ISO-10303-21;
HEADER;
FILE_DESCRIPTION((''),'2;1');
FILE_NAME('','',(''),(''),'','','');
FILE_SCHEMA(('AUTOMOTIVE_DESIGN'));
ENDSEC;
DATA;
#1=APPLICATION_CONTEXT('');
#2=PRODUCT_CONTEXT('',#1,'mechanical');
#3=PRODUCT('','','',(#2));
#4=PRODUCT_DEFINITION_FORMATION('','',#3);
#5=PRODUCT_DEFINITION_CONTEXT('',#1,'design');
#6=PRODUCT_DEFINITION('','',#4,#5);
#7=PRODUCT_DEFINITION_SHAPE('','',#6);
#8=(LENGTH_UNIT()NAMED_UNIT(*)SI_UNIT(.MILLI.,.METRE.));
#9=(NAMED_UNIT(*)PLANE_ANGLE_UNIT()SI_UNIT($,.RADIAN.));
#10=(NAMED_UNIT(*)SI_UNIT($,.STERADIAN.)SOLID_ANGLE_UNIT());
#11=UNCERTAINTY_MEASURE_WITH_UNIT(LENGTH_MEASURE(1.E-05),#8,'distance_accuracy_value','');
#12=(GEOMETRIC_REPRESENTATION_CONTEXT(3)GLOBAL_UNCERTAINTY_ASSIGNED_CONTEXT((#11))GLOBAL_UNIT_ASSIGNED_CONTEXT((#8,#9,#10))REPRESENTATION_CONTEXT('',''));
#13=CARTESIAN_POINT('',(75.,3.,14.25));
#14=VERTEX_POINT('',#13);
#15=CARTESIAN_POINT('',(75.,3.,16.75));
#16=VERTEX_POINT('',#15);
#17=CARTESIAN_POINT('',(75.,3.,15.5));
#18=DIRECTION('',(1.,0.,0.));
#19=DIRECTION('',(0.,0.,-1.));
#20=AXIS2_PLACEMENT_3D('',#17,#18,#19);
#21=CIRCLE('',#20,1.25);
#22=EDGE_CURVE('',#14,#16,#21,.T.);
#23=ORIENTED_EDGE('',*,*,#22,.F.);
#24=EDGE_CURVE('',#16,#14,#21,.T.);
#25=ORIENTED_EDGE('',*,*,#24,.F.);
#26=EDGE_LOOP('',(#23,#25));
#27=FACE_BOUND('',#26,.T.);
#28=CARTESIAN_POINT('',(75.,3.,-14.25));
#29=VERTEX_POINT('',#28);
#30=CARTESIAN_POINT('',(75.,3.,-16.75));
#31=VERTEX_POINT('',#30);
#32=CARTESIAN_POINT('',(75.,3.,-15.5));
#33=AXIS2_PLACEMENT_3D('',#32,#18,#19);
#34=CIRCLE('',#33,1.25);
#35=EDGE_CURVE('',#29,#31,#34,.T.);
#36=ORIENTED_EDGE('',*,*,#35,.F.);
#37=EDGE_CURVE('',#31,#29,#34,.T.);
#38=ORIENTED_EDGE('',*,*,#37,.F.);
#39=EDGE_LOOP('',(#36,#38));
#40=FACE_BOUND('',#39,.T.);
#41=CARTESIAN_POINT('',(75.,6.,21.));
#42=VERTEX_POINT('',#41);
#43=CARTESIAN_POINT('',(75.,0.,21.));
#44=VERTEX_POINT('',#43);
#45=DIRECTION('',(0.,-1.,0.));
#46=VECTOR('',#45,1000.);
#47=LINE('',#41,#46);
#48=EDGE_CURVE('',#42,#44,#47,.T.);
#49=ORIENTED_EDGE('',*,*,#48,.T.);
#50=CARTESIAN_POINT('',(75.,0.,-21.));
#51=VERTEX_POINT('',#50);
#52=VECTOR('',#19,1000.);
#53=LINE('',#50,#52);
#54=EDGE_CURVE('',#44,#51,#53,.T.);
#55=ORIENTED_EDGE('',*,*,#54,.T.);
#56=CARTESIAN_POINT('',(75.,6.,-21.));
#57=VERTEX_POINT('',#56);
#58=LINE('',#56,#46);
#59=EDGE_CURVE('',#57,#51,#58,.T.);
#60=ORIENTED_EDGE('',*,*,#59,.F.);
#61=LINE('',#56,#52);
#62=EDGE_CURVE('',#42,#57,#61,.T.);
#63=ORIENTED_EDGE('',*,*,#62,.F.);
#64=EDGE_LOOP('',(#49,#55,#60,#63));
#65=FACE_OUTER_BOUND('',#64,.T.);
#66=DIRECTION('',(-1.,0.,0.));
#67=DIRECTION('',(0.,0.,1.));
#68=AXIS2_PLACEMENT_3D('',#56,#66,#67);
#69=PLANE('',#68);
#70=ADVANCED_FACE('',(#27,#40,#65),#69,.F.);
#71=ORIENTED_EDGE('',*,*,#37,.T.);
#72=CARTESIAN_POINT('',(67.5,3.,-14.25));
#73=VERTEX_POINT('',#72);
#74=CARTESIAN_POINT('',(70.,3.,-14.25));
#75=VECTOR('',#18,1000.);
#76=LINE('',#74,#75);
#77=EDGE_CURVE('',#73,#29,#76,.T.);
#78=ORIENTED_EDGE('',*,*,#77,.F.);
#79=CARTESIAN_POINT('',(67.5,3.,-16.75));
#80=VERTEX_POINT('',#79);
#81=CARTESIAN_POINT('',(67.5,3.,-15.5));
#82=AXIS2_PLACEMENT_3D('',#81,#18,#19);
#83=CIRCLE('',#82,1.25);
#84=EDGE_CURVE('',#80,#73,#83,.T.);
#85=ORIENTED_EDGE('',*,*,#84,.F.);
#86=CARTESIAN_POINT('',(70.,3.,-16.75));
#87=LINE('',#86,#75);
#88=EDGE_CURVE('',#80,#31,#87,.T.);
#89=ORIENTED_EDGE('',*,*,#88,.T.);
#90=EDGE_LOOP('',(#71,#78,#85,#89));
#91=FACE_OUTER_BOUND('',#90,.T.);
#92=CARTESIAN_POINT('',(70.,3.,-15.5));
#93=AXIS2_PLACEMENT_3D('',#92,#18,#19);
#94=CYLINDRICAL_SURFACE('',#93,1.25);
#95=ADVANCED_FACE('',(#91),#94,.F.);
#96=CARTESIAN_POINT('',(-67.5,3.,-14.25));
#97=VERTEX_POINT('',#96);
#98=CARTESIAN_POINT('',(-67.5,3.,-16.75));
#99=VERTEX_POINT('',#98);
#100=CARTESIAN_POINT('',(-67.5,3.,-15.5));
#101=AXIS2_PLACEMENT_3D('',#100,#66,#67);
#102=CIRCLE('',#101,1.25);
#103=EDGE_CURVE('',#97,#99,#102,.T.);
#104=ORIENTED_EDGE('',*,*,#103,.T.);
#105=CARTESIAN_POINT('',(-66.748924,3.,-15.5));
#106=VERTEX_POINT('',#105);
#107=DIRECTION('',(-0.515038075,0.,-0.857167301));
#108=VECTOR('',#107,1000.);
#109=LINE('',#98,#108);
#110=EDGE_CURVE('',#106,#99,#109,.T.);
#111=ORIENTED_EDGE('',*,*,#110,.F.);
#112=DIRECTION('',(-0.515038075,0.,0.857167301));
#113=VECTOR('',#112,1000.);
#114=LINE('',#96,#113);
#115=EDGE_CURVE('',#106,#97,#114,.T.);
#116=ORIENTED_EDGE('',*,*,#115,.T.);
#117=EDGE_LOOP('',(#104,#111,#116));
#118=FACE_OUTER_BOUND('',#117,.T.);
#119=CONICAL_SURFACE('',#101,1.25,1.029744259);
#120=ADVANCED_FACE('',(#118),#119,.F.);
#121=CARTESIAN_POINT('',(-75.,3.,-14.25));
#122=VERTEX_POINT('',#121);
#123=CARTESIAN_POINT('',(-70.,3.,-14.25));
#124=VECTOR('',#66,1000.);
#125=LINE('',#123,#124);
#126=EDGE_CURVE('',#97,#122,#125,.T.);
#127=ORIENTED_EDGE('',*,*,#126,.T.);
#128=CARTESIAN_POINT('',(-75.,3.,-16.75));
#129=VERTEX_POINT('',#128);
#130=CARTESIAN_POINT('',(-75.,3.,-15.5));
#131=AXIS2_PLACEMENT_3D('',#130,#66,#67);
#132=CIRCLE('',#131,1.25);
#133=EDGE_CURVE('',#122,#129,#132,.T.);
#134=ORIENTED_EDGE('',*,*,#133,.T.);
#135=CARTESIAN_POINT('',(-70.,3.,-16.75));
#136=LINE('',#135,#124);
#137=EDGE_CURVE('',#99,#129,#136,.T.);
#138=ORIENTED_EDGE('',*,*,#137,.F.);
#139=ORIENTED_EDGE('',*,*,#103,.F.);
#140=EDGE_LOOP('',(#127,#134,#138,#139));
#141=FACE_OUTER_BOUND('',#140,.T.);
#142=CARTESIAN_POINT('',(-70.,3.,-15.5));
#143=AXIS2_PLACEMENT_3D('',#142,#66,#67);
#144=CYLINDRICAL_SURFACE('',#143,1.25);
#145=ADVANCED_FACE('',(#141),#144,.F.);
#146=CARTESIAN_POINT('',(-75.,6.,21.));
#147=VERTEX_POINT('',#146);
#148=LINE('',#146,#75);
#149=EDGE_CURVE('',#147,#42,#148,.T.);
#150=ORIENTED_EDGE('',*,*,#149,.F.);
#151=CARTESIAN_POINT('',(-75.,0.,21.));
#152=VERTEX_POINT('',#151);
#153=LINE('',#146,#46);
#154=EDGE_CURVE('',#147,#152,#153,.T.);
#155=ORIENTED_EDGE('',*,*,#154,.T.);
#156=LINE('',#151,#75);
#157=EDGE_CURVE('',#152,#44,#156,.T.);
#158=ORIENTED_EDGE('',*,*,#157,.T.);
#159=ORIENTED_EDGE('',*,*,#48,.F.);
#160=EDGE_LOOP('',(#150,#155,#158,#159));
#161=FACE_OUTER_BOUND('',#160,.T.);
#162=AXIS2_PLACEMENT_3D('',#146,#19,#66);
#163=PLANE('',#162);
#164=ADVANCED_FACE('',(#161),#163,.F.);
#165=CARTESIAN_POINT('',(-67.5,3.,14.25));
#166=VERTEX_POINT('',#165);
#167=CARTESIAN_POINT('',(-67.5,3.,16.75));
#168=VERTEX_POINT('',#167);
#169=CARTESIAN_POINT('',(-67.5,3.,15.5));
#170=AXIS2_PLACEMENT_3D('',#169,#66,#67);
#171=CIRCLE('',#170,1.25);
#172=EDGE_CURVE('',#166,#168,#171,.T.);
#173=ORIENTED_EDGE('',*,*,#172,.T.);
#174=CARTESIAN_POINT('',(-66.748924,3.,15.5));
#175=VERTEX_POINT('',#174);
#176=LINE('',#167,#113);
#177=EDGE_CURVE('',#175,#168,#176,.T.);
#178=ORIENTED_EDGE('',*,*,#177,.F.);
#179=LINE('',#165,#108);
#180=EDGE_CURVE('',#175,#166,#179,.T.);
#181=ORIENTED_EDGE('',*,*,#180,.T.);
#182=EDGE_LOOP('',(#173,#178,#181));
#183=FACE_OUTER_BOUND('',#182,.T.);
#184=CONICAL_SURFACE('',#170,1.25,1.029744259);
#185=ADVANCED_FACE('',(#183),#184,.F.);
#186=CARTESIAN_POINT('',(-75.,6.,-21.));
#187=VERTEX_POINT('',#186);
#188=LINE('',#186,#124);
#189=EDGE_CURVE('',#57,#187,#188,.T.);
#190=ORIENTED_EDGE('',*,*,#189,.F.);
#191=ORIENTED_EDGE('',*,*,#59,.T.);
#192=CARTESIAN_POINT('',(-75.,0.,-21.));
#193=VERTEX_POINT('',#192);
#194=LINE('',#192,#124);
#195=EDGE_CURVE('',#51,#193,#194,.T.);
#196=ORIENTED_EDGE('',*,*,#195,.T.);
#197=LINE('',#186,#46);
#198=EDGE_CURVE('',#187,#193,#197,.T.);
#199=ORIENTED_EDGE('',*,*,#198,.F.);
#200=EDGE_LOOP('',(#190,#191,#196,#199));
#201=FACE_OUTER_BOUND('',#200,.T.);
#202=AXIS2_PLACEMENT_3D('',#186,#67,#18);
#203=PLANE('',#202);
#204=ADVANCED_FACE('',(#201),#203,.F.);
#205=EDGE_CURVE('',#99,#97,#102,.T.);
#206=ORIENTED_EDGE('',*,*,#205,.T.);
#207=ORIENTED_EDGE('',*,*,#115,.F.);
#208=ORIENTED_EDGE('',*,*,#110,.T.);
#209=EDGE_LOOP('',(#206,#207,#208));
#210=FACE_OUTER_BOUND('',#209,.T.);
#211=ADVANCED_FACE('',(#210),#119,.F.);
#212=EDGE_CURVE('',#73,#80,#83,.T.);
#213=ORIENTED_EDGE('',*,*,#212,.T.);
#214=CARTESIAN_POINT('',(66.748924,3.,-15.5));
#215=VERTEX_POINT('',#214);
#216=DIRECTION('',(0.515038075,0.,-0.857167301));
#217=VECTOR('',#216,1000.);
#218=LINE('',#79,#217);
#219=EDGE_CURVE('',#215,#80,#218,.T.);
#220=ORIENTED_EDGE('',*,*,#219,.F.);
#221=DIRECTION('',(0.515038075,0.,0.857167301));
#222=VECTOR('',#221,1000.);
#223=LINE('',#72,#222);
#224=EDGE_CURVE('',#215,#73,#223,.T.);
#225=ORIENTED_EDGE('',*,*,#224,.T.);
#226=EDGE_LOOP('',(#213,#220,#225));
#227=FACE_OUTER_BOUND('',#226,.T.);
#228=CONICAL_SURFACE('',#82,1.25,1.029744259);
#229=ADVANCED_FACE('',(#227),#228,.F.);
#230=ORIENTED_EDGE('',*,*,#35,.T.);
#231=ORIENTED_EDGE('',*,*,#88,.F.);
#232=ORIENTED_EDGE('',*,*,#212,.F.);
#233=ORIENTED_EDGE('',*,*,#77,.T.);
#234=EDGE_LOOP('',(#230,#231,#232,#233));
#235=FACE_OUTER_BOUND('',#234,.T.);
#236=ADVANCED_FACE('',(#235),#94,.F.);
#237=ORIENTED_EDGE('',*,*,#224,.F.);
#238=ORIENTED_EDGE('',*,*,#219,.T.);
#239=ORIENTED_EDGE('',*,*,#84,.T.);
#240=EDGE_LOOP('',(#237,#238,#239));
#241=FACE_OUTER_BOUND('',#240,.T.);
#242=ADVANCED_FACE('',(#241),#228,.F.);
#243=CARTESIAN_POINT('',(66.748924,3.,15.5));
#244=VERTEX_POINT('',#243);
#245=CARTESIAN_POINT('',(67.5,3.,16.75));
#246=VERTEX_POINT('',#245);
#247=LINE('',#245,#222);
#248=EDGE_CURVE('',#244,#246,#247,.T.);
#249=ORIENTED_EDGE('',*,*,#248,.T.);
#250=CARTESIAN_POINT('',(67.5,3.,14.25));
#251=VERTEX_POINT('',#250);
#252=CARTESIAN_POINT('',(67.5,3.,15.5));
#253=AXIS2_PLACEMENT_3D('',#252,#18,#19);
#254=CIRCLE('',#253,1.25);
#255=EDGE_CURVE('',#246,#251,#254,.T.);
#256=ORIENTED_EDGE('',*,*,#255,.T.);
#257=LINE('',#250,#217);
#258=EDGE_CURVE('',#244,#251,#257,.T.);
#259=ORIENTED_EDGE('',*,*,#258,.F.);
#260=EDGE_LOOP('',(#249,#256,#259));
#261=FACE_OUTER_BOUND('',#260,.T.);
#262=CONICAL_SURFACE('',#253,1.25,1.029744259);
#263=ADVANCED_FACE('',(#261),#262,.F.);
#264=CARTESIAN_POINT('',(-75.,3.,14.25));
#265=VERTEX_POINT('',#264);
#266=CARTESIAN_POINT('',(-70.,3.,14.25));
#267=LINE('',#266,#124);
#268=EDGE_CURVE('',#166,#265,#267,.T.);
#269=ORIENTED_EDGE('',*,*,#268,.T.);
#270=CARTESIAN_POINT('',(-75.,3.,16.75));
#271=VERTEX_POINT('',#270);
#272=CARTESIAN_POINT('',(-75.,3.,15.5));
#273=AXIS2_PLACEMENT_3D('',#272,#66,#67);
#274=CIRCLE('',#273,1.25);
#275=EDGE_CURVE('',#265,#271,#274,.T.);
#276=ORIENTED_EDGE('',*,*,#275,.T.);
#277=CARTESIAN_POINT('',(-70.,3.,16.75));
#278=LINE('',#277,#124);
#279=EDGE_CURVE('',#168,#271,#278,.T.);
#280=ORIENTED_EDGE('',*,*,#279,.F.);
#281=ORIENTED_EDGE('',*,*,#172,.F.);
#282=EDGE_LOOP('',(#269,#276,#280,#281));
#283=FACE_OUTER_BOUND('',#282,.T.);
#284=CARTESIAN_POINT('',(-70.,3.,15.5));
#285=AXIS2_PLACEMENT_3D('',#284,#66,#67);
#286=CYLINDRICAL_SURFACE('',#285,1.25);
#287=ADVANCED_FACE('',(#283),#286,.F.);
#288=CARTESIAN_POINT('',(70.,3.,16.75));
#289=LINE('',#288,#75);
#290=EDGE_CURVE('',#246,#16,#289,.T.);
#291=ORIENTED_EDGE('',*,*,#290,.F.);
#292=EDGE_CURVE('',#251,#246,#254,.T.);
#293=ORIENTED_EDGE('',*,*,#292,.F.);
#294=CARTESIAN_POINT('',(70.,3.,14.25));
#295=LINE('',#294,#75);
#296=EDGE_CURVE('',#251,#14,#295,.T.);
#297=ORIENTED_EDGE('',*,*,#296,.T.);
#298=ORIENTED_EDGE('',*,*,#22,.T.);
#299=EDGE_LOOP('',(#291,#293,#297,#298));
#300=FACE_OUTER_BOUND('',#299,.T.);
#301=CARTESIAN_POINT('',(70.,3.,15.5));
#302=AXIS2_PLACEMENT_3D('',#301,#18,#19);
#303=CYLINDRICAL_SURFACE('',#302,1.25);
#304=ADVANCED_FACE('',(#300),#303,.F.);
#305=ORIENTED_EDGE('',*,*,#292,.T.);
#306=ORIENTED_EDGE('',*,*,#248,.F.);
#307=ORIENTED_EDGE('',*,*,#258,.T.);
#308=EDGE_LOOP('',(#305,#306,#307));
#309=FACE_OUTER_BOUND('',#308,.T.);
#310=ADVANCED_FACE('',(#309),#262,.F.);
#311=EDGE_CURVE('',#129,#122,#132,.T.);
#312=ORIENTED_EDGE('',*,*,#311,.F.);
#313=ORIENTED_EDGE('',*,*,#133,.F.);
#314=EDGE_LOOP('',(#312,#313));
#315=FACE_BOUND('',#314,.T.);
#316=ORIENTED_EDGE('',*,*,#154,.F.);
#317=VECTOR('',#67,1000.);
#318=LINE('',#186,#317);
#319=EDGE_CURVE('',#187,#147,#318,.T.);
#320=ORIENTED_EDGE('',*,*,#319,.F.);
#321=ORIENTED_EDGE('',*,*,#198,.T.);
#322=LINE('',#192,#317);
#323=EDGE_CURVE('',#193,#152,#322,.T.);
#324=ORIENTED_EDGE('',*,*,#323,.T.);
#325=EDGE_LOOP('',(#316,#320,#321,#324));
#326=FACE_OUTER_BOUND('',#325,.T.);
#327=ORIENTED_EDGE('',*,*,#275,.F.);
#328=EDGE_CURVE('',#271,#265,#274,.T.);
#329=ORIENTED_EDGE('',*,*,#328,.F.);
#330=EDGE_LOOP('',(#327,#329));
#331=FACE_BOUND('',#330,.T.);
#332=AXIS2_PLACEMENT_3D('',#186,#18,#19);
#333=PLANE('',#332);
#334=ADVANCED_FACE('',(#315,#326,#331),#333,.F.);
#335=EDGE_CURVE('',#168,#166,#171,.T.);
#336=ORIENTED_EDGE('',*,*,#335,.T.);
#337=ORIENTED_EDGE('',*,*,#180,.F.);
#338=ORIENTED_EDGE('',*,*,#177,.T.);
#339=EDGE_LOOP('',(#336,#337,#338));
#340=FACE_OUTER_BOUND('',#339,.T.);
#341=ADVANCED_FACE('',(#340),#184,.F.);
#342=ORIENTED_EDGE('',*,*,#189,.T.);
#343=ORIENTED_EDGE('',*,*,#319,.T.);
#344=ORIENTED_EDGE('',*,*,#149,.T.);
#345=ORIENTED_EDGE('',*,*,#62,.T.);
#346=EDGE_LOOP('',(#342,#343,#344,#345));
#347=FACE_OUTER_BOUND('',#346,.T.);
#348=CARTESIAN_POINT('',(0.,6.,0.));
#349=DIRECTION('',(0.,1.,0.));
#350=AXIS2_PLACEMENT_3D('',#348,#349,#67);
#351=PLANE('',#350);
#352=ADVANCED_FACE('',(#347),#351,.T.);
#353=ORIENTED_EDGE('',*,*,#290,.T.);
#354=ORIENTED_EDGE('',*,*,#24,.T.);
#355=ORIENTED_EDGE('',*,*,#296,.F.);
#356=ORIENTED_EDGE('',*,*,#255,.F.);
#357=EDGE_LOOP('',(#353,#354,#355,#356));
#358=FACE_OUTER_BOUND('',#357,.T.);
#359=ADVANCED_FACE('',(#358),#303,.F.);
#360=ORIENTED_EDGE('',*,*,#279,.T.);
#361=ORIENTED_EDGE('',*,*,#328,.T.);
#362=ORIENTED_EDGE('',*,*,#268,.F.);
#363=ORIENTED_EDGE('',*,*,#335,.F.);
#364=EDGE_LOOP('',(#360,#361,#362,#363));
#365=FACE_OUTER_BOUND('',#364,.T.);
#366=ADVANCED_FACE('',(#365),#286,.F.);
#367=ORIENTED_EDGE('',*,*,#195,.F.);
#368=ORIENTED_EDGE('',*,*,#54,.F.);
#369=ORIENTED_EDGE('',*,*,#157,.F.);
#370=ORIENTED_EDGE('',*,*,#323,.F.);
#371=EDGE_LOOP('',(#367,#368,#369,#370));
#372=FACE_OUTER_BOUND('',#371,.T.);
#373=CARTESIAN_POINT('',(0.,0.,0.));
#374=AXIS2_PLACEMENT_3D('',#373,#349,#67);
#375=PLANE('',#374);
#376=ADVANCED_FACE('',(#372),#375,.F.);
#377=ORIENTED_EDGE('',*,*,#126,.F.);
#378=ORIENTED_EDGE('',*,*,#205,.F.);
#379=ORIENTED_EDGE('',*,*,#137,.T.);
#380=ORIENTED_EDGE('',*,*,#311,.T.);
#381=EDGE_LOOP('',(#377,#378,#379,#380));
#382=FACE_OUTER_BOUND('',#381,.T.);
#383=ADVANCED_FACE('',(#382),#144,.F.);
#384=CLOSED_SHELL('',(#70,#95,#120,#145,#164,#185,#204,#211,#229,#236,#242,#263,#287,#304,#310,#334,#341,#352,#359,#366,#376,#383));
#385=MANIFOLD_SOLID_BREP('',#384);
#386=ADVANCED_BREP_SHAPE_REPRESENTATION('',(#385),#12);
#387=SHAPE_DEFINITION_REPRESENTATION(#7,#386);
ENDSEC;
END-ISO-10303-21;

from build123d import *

# Parameters (mm, degrees)
SKETCH1_W             = 150
SKETCH1_H             = 42
BOSS_EXTRUDE1_DEPTH   = 6
SKETCH2_R             = 1.25
CUT_EXTRUDE1_DEPTH    = 5
CUT_EXTRUDE2_START    = -5
SKETCH3_R             = 1.25
CUT_EXTRUDE2_DEPTH    = 5
M3_TAPPED_HOLE1_D     = 2.5
M3_TAPPED_HOLE1_DEPTH = 7.5
M3_TAPPED_HOLE1_TIP   = 0.751075774
M3_TAPPED_HOLE2_D     = 2.5
M3_TAPPED_HOLE2_DEPTH = 7.5
M3_TAPPED_HOLE2_TIP   = 0.751075774


with BuildPart() as part:
    # Sketch1 → Boss-Extrude1 (new body)
    with BuildSketch(Plane(origin=(0, 0, 0), x_dir=(1, 0, 0), z_dir=(0, 1, 0))):
        Rectangle(SKETCH1_W, SKETCH1_H)
    extrude(amount=BOSS_EXTRUDE1_DEPTH)

    # Sketch2 → Cut-Extrude1 (cut)
    with BuildSketch(Plane(origin=(75, 0, 0), x_dir=(0, 0, -1), z_dir=(1, 0, 0))):
        with Locations((15.5, 3)):
            Circle(SKETCH2_R)
        with Locations((-15.5, 3)):
            Circle(SKETCH2_R)
    extrude(amount=-CUT_EXTRUDE1_DEPTH, mode=Mode.SUBTRACT)

    # Sketch3 → Cut-Extrude2 (cut)
    with BuildSketch(Plane.ZY.offset(75).offset(CUT_EXTRUDE2_START)):
        with Locations(Location((-15.5, 3, 0), (0, 0, 180))):
            Circle(SKETCH3_R)
        with Locations(Location((15.5, 3, 0), (0, 0, 180))):
            Circle(SKETCH3_R)
    extrude(amount=CUT_EXTRUDE2_DEPTH, mode=Mode.SUBTRACT)

    # M3 Tapped Hole1
    with Locations(Plane(origin=(75, 0, 0), x_dir=(0, 0, -1), z_dir=(1, 0, 0))):
        with Locations((-15.5, 3), (15.5, 3)):
            Hole(M3_TAPPED_HOLE1_D / 2, depth=M3_TAPPED_HOLE1_DEPTH)
            with Locations((0, 0, -(M3_TAPPED_HOLE1_DEPTH + M3_TAPPED_HOLE1_TIP / 2))):  # 118° drill point
                Cone(0, M3_TAPPED_HOLE1_D / 2, M3_TAPPED_HOLE1_TIP, mode=Mode.SUBTRACT)

    # M3 Tapped Hole2
    with Locations(Plane.ZY.offset(75)):
        with Locations((-15.5, 3), (15.5, 3)):
            Hole(M3_TAPPED_HOLE2_D / 2, depth=M3_TAPPED_HOLE2_DEPTH)
            with Locations((0, 0, -(M3_TAPPED_HOLE2_DEPTH + M3_TAPPED_HOLE2_TIP / 2))):  # 118° drill point
                Cone(0, M3_TAPPED_HOLE2_D / 2, M3_TAPPED_HOLE2_TIP, mode=Mode.SUBTRACT)


solid = part.part
